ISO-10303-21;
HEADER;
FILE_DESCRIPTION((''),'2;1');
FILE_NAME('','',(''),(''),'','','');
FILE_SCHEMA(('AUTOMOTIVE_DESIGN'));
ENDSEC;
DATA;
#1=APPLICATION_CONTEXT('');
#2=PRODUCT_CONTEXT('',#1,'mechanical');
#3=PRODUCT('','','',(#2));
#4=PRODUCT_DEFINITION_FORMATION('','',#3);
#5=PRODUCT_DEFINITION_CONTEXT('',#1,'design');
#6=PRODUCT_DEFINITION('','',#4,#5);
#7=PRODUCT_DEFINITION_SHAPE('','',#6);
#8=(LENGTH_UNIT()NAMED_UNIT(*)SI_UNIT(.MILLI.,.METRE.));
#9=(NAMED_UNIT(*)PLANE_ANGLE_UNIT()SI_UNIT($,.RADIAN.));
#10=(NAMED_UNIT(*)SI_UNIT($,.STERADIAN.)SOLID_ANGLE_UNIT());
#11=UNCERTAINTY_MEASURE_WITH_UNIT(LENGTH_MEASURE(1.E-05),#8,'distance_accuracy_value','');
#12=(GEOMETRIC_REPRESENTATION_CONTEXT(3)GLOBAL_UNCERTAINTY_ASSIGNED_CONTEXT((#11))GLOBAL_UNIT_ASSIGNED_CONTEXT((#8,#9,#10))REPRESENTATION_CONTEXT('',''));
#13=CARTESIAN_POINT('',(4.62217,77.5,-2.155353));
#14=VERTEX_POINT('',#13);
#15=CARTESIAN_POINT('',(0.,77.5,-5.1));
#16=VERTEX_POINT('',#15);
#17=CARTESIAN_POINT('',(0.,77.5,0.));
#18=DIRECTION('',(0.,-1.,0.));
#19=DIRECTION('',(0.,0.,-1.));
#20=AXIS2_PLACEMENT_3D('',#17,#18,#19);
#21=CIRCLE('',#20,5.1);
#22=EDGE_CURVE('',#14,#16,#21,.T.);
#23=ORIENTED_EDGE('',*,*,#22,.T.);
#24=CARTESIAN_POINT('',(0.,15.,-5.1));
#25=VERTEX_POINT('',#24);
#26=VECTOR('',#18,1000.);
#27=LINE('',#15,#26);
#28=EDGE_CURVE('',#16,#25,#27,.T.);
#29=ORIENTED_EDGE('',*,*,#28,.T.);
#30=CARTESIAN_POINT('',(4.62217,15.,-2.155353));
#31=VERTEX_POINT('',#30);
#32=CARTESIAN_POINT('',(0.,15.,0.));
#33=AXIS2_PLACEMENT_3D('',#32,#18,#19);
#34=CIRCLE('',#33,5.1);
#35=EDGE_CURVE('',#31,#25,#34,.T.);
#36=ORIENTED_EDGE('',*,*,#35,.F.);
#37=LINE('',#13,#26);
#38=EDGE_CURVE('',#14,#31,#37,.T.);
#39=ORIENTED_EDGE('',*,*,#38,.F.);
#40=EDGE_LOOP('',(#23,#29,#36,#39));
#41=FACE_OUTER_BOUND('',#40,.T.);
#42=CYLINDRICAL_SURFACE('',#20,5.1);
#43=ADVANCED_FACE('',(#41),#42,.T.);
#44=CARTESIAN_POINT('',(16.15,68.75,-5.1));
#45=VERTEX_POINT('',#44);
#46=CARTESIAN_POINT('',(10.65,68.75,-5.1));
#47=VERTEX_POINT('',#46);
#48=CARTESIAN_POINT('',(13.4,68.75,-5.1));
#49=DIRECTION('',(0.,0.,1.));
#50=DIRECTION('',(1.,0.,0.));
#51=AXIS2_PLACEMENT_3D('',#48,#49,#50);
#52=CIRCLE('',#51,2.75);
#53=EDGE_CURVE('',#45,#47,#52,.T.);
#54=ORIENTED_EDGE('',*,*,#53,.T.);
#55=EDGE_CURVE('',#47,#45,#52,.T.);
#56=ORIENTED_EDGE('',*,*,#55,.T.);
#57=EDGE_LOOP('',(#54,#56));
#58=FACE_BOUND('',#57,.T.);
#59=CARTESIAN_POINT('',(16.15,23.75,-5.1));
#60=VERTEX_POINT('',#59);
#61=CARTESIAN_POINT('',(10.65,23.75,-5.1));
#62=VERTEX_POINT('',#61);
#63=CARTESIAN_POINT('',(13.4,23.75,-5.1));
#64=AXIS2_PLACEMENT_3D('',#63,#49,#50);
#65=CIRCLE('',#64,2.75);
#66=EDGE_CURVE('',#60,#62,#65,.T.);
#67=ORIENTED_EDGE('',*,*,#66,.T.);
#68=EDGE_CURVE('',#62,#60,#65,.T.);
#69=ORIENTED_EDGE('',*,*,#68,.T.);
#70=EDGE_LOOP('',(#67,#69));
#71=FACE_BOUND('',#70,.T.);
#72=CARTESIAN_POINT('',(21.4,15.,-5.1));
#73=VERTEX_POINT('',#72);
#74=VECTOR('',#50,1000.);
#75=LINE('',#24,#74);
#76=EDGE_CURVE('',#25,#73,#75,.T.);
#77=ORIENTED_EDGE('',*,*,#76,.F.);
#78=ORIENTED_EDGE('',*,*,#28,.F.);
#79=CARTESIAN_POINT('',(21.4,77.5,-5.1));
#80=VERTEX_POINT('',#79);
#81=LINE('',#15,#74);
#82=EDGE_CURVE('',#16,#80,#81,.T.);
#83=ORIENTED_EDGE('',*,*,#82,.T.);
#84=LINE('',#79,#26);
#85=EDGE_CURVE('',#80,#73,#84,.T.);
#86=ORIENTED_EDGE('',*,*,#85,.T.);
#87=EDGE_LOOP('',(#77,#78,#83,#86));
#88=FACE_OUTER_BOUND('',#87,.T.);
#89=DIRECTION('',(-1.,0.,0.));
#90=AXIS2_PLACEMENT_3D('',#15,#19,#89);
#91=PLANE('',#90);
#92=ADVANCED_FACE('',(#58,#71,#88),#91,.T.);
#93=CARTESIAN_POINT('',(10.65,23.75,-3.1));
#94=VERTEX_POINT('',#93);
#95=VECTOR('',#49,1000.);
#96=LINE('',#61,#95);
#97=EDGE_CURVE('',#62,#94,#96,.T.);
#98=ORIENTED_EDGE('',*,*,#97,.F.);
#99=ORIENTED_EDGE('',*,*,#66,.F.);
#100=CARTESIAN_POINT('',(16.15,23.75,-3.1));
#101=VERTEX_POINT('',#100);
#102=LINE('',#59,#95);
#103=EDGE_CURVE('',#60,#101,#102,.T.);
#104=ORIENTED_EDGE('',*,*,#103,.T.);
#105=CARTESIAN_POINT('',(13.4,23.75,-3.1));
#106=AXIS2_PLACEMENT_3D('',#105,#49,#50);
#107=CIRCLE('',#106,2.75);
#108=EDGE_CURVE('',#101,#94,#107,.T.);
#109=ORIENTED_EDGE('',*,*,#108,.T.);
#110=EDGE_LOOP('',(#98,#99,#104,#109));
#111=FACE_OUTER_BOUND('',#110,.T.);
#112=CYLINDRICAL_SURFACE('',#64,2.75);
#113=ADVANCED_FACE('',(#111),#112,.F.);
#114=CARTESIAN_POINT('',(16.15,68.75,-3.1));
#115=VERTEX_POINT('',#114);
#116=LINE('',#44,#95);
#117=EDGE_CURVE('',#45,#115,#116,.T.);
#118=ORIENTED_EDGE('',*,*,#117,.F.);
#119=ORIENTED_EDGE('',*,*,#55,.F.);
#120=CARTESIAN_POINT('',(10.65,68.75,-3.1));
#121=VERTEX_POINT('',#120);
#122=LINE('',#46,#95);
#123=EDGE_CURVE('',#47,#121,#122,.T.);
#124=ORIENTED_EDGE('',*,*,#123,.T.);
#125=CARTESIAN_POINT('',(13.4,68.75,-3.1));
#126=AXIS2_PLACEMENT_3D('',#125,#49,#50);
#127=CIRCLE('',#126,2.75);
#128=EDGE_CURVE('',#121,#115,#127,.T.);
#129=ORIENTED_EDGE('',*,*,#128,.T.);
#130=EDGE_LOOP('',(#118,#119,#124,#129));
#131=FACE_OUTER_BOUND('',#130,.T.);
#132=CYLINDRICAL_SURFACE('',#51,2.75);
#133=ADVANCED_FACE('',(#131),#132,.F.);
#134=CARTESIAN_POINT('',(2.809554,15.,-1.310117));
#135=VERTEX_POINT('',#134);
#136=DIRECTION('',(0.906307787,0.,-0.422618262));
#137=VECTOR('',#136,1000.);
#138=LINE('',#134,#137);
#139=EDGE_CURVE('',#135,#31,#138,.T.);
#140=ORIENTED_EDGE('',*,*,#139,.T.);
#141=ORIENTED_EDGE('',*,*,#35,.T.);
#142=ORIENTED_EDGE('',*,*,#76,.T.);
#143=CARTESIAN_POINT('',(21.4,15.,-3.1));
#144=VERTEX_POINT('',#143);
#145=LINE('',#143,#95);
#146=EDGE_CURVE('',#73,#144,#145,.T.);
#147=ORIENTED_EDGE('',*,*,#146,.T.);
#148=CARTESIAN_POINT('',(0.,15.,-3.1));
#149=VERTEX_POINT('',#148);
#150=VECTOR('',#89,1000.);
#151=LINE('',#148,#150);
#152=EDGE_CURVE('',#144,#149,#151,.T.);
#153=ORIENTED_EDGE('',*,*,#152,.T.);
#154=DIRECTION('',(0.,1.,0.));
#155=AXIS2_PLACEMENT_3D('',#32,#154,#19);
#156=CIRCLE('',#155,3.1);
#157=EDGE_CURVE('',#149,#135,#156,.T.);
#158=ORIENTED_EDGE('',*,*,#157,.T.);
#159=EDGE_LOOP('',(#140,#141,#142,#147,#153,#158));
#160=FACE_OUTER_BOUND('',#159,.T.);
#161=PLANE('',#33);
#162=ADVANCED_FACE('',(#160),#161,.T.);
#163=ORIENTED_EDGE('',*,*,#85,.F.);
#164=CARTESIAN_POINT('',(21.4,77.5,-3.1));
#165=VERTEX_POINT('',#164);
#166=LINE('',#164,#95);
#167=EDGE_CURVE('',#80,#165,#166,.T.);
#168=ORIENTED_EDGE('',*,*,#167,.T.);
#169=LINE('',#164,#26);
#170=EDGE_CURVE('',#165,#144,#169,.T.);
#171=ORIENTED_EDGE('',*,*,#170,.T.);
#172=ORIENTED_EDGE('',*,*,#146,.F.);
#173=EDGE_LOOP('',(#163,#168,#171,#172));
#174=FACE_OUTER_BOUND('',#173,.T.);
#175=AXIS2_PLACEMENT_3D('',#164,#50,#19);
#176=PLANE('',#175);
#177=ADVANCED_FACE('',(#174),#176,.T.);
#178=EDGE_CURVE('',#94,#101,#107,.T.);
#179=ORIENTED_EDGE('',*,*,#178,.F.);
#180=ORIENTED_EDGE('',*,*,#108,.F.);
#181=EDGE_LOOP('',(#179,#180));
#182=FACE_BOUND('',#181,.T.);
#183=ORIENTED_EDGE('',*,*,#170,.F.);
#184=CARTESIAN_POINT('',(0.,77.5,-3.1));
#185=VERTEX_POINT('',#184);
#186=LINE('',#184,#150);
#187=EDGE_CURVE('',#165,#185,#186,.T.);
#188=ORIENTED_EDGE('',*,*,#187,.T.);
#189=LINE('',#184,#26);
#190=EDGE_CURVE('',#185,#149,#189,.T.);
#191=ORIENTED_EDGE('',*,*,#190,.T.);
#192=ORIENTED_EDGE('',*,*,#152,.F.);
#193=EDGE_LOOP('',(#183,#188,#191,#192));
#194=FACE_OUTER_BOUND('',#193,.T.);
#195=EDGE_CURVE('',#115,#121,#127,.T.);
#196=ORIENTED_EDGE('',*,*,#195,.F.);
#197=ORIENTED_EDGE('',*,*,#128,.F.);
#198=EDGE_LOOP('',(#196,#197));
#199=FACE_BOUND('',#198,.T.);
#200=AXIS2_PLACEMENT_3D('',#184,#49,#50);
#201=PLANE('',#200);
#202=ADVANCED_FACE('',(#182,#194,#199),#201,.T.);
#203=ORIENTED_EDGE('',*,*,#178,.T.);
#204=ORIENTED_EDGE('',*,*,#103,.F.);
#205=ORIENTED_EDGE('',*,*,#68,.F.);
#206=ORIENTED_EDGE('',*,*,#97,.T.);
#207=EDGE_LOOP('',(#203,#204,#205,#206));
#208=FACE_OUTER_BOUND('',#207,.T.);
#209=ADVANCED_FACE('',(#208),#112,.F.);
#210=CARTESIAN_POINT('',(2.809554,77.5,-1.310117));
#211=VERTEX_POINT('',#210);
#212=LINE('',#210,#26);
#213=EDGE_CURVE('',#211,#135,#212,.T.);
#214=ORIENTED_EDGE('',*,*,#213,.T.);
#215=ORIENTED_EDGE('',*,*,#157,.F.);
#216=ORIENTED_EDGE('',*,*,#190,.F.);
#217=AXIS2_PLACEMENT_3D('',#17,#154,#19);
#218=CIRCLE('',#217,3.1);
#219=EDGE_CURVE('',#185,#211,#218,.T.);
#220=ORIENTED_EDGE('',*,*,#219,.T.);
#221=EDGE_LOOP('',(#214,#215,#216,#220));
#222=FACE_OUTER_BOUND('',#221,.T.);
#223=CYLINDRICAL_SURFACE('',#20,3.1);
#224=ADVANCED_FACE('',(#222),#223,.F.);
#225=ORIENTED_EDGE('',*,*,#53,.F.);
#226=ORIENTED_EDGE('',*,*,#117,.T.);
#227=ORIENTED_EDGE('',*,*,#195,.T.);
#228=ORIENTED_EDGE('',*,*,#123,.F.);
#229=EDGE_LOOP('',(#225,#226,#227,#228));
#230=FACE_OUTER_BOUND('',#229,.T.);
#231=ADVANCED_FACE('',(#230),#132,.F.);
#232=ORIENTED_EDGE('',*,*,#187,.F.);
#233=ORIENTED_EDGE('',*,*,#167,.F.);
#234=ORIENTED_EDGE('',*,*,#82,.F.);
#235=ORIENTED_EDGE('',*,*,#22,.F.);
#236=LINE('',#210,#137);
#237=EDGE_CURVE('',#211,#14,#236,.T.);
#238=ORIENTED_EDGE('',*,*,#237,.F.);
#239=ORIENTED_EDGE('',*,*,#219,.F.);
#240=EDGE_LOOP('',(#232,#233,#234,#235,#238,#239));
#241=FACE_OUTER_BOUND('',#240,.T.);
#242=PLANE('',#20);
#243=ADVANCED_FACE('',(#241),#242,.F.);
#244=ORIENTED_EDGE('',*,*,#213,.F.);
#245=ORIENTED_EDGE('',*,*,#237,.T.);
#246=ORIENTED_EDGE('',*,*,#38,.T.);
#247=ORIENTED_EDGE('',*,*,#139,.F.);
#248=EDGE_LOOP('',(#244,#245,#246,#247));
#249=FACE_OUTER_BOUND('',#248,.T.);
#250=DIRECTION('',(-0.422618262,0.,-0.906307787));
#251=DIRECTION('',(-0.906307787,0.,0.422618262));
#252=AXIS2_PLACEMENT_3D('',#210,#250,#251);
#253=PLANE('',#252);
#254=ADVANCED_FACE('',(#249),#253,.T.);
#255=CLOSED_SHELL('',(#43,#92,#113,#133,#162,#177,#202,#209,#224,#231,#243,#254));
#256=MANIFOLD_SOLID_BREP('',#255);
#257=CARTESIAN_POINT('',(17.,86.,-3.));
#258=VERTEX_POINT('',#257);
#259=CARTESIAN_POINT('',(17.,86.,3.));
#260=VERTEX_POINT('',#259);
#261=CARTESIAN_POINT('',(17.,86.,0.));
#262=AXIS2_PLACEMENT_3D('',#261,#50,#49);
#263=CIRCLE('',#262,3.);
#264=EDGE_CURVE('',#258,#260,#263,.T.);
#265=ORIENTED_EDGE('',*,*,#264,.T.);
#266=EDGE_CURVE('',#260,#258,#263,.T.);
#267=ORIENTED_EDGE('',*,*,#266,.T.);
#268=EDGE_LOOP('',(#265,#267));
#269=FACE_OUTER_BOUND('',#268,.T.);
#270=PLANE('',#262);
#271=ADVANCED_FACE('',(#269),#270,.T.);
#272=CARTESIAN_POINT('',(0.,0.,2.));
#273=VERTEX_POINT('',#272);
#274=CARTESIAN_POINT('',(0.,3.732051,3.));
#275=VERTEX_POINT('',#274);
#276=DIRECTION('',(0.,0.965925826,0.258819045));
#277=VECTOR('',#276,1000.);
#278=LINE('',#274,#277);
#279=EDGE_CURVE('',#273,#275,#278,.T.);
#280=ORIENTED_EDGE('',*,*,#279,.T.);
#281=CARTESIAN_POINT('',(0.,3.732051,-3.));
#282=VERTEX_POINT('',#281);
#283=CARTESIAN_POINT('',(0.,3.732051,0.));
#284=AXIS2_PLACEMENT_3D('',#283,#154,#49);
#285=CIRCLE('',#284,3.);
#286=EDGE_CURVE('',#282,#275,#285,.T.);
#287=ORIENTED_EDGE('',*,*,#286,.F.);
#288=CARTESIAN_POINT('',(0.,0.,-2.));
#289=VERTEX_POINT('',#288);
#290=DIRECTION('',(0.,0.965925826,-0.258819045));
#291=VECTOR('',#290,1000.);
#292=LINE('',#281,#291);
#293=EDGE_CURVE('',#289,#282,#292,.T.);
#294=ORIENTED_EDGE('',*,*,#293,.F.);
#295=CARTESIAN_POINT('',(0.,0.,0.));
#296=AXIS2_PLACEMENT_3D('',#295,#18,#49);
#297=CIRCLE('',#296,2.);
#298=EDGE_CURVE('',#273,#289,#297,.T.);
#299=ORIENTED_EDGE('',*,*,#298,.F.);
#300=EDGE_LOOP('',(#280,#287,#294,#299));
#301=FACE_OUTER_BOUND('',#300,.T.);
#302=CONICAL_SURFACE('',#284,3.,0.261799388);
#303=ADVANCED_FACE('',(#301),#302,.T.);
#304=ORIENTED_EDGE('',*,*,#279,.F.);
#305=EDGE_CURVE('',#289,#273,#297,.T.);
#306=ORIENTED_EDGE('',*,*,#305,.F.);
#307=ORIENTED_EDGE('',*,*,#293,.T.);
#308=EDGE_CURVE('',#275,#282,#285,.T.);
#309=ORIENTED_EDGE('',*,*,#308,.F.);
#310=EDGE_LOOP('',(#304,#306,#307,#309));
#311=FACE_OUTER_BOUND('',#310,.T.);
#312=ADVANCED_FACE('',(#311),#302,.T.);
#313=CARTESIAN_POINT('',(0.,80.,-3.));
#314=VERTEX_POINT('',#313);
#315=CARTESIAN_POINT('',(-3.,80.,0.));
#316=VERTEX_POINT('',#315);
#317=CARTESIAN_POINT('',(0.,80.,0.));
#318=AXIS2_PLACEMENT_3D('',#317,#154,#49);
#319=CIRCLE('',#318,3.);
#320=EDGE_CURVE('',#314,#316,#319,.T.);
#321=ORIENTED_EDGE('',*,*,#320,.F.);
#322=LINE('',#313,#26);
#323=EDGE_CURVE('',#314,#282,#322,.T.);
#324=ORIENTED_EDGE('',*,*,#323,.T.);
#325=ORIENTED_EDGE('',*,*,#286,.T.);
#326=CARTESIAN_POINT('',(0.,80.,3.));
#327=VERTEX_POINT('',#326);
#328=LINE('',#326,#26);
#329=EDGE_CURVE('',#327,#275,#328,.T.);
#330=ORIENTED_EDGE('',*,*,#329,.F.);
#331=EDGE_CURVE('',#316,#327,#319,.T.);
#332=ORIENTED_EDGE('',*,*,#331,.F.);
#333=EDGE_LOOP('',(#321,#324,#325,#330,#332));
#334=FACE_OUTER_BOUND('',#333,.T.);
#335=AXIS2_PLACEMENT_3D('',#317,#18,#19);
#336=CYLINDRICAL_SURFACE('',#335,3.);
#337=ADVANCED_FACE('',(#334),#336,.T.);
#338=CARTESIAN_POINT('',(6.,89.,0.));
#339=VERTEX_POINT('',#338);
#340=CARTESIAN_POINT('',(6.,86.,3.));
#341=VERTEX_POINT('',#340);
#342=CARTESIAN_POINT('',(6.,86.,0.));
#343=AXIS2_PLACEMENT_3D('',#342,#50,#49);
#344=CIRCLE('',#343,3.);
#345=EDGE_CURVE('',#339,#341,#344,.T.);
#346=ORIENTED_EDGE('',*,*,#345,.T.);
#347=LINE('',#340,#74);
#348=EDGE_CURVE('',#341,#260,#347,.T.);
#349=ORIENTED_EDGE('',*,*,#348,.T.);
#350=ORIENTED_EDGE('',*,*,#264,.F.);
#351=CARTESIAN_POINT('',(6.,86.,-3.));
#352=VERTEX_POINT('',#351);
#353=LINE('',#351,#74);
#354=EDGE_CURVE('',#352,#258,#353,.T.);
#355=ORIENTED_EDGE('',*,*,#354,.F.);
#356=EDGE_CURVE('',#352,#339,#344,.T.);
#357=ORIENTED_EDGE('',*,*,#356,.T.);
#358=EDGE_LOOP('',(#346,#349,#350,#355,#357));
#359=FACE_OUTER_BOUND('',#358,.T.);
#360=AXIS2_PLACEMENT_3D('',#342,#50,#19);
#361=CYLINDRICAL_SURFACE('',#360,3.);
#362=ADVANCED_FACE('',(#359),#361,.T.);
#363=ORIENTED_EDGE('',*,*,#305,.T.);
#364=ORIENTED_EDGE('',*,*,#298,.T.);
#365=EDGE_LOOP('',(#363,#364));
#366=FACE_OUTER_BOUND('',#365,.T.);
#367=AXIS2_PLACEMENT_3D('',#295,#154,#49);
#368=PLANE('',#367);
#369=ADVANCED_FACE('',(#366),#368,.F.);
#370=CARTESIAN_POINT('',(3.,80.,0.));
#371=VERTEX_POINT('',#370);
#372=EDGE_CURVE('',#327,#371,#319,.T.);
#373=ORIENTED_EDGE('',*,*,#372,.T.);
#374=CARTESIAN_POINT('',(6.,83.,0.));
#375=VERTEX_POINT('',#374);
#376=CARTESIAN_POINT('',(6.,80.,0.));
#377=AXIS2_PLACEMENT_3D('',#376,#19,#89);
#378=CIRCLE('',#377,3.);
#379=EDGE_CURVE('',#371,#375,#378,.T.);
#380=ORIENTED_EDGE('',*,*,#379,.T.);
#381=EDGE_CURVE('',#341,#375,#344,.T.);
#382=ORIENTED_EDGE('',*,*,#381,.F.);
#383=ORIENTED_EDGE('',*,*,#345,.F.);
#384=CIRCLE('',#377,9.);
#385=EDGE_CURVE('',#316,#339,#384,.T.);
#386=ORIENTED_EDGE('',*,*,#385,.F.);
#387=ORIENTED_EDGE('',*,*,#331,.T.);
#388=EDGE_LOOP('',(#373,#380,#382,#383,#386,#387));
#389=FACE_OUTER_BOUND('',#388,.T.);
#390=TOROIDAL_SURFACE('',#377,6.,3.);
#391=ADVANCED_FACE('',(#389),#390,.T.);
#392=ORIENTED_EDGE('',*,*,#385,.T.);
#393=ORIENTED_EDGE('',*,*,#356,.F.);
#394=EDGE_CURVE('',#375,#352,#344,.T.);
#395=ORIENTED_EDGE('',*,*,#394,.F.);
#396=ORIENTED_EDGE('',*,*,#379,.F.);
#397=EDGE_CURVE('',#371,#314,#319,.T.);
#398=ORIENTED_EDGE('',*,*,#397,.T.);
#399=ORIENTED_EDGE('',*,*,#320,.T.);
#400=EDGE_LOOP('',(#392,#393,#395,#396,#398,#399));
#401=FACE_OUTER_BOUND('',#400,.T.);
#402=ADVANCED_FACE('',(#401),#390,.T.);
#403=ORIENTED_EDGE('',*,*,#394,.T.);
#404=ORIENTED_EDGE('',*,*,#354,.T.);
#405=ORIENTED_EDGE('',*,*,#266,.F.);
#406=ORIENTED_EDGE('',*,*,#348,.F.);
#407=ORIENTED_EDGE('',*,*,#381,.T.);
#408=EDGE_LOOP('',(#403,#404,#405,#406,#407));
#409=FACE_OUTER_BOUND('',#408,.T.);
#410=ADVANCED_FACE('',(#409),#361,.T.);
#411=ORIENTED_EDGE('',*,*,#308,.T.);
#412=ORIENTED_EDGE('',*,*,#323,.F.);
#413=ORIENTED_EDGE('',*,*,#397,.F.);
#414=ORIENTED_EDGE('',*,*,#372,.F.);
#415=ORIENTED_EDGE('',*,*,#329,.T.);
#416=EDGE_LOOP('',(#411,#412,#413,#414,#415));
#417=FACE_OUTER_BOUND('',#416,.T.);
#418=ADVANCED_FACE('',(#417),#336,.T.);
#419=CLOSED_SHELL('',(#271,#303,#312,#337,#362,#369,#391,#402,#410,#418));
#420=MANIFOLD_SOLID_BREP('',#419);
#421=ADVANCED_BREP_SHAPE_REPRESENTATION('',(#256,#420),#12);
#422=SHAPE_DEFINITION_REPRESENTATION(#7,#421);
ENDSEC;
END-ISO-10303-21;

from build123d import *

# Parameters (mm, degrees)
SKETCH_2_R          = 3
EXTRUDE_1_DEPTH     = 62.5
SKETCH_5_R          = 2.75
CUT_EXTRUDE_2_DEPTH = 92.903210052
CHAMFER_1_SIZE      = 1
CHAMFER_1_SIZE2     = 3.732050808


with BuildPart() as part:
    # 扫描1: sweep along a path in 草图1
    with BuildLine(Plane.XY) as sweep_1_path:
        Line((0, 0), (0, 80))
        ThreePointArc((0, 80), (1.757359313, 84.242640687), (6, 86))
        Line((6, 86), (17, 86))
    # 草图2 → 扫描1 (sweep)
    with BuildSketch(Plane(origin=(0, 0, 0), x_dir=(1, 0, 0), z_dir=(0, 1, 0))):
        Circle(SKETCH_2_R)
    sweep(path=sweep_1_path.line)

    # 倒角1
    chamfer_1_edges = [part.edges().sort_by_distance(p)[0] for p in [
        (-3, 0, 0),
    ]]
    chamfer_1_side = [part.faces().sort_by_distance(p)[0] for p in [
        (0, 0, 0),
    ]]
    chamfer(chamfer_1_edges, length=CHAMFER_1_SIZE, length2=CHAMFER_1_SIZE2, reference=chamfer_1_side[0])


with BuildPart() as body_2:
    # 草图3 → 凸台-拉伸1 (new body)
    with BuildSketch(Plane(origin=(0, 15, 0), x_dir=(-1, 0, 0), z_dir=(0, -1, 0))):
        with BuildLine():
            Line((0, 3.1), (-21.4, 3.1))
            Line((-21.4, 3.1), (-21.4, 5.1))
            Line((-21.4, 5.1), (0, 5.1))
            ThreePointArc((0, 5.1), (2.740228003, -4.301296374), (-4.622169714, 2.155353135))
            Line((-4.622169714, 2.155353135), (-2.80955414, 1.310116611))
            ThreePointArc((-2.80955414, 1.310116611), (1.665628786, -2.614513482), (0, 3.1))
        make_face()
    extrude(amount=-EXTRUDE_1_DEPTH)

    # 草图5 → 切除-拉伸2 (cut, through all)
    with BuildSketch(Plane.XY.offset(-3.1)):
        with Locations((13.4, 23.75)):
            Circle(SKETCH_5_R)
        with Locations((13.4, 68.75)):
            Circle(SKETCH_5_R)
    extrude(amount=-CUT_EXTRUDE_2_DEPTH, mode=Mode.SUBTRACT)


solid = Compound([part.part, body_2.part])
